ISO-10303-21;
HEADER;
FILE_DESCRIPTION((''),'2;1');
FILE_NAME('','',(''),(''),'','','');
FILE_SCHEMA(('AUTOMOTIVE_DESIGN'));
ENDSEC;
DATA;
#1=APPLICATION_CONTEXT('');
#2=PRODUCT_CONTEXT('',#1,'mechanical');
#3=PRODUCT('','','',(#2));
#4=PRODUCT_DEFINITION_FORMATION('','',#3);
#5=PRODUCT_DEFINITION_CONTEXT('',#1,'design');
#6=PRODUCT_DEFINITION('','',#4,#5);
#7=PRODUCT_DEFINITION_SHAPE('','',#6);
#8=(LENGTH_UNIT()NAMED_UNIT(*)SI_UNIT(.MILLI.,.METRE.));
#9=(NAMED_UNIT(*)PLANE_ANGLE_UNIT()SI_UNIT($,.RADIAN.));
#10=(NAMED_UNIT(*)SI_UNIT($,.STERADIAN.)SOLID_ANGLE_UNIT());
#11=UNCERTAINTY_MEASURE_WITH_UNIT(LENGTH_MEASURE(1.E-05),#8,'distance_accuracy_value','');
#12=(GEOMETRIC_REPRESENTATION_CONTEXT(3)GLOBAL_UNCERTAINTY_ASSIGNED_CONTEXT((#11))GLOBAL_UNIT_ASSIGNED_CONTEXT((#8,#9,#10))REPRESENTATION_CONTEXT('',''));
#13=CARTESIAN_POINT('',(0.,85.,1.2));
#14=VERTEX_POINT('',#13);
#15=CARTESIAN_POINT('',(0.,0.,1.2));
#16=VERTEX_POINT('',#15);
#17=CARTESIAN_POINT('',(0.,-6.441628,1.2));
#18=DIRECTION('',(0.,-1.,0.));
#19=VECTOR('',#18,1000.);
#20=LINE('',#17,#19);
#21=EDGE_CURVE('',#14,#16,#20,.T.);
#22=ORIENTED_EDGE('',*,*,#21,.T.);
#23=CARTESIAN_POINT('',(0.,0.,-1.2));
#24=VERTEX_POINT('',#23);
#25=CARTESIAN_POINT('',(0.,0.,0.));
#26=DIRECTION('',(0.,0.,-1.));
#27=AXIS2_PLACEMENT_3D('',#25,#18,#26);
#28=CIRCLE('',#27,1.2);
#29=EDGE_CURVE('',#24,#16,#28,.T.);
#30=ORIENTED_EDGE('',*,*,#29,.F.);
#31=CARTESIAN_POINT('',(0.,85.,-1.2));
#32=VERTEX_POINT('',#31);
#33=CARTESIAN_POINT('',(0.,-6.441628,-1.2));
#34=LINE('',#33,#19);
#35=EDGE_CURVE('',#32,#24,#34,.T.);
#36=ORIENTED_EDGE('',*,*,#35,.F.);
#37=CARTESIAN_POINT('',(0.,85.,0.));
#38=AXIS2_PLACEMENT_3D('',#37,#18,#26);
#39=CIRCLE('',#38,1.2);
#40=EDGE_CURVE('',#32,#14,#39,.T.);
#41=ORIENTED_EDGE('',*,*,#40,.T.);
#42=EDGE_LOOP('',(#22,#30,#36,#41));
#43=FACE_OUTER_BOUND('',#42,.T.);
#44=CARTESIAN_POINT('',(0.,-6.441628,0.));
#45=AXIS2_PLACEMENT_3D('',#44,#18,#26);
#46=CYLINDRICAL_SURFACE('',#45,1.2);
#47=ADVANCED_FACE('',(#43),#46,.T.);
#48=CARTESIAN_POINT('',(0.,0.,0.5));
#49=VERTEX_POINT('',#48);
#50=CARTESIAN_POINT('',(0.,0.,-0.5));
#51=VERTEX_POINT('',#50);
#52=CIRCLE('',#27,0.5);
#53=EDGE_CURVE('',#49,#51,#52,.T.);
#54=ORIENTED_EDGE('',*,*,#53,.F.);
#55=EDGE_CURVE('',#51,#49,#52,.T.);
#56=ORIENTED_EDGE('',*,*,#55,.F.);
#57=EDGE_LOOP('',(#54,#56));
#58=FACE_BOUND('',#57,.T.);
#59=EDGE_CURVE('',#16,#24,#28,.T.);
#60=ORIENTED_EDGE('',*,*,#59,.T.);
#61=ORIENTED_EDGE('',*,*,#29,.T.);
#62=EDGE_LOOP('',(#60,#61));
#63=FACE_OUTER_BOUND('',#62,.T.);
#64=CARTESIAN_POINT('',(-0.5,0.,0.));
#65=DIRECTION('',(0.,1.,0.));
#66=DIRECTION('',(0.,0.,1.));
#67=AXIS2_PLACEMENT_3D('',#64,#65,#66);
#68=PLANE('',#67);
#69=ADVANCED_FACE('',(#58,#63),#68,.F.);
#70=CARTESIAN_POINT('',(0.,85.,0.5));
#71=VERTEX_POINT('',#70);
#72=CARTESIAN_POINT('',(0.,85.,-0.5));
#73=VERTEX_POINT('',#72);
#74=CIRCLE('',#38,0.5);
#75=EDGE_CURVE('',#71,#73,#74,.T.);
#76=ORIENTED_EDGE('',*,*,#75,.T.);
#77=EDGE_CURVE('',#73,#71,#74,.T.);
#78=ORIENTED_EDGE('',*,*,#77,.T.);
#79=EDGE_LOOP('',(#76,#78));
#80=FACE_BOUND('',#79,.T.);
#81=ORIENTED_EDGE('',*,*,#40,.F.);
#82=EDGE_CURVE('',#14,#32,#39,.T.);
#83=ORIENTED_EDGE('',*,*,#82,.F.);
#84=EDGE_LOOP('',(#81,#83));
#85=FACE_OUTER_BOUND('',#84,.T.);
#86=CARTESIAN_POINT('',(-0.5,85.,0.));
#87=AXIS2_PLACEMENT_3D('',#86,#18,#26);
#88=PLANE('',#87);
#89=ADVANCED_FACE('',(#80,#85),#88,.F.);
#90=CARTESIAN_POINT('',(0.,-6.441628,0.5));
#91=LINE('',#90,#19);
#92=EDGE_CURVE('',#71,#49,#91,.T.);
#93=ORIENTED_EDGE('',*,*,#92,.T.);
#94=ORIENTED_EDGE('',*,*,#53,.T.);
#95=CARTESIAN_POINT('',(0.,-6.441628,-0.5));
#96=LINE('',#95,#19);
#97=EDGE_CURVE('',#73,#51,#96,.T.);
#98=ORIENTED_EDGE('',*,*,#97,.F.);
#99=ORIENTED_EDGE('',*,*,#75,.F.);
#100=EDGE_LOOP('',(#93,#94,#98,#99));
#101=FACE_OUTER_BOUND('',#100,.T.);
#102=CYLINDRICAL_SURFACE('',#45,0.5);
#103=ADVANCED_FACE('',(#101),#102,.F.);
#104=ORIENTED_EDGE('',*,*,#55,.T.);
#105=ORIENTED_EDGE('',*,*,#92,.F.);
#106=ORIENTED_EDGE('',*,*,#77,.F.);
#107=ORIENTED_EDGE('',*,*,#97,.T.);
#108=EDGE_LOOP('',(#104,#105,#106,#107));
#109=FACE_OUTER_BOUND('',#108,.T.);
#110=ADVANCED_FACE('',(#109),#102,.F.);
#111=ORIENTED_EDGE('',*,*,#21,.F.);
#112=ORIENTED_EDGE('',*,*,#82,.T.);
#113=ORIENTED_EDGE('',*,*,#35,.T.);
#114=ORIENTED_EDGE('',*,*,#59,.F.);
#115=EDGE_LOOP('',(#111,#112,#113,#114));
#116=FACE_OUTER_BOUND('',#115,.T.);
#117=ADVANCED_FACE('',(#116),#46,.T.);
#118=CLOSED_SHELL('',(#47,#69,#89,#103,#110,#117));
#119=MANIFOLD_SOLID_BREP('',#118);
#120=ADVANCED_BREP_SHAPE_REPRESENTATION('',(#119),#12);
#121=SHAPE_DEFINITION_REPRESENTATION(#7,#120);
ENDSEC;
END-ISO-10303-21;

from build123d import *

# Parameters (mm, degrees)
SKETCH1_W = 0.7
SKETCH1_H = 85


with BuildPart() as part:
    # Sketch1 → Revolve1 (revolve)
    with BuildSketch(Plane.XY, mode=Mode.PRIVATE) as revolve1_sk:
        with Locations((-0.85, 42.5)):
            Rectangle(SKETCH1_W, SKETCH1_H)
    revolve(revolve1_sk.sketch.rotate(Axis((0, -6.441627678, 0), (0, 1, 0)), 270), axis=Axis((0, -6.441627678, 0), (0, 1, 0)))


solid = part.part
